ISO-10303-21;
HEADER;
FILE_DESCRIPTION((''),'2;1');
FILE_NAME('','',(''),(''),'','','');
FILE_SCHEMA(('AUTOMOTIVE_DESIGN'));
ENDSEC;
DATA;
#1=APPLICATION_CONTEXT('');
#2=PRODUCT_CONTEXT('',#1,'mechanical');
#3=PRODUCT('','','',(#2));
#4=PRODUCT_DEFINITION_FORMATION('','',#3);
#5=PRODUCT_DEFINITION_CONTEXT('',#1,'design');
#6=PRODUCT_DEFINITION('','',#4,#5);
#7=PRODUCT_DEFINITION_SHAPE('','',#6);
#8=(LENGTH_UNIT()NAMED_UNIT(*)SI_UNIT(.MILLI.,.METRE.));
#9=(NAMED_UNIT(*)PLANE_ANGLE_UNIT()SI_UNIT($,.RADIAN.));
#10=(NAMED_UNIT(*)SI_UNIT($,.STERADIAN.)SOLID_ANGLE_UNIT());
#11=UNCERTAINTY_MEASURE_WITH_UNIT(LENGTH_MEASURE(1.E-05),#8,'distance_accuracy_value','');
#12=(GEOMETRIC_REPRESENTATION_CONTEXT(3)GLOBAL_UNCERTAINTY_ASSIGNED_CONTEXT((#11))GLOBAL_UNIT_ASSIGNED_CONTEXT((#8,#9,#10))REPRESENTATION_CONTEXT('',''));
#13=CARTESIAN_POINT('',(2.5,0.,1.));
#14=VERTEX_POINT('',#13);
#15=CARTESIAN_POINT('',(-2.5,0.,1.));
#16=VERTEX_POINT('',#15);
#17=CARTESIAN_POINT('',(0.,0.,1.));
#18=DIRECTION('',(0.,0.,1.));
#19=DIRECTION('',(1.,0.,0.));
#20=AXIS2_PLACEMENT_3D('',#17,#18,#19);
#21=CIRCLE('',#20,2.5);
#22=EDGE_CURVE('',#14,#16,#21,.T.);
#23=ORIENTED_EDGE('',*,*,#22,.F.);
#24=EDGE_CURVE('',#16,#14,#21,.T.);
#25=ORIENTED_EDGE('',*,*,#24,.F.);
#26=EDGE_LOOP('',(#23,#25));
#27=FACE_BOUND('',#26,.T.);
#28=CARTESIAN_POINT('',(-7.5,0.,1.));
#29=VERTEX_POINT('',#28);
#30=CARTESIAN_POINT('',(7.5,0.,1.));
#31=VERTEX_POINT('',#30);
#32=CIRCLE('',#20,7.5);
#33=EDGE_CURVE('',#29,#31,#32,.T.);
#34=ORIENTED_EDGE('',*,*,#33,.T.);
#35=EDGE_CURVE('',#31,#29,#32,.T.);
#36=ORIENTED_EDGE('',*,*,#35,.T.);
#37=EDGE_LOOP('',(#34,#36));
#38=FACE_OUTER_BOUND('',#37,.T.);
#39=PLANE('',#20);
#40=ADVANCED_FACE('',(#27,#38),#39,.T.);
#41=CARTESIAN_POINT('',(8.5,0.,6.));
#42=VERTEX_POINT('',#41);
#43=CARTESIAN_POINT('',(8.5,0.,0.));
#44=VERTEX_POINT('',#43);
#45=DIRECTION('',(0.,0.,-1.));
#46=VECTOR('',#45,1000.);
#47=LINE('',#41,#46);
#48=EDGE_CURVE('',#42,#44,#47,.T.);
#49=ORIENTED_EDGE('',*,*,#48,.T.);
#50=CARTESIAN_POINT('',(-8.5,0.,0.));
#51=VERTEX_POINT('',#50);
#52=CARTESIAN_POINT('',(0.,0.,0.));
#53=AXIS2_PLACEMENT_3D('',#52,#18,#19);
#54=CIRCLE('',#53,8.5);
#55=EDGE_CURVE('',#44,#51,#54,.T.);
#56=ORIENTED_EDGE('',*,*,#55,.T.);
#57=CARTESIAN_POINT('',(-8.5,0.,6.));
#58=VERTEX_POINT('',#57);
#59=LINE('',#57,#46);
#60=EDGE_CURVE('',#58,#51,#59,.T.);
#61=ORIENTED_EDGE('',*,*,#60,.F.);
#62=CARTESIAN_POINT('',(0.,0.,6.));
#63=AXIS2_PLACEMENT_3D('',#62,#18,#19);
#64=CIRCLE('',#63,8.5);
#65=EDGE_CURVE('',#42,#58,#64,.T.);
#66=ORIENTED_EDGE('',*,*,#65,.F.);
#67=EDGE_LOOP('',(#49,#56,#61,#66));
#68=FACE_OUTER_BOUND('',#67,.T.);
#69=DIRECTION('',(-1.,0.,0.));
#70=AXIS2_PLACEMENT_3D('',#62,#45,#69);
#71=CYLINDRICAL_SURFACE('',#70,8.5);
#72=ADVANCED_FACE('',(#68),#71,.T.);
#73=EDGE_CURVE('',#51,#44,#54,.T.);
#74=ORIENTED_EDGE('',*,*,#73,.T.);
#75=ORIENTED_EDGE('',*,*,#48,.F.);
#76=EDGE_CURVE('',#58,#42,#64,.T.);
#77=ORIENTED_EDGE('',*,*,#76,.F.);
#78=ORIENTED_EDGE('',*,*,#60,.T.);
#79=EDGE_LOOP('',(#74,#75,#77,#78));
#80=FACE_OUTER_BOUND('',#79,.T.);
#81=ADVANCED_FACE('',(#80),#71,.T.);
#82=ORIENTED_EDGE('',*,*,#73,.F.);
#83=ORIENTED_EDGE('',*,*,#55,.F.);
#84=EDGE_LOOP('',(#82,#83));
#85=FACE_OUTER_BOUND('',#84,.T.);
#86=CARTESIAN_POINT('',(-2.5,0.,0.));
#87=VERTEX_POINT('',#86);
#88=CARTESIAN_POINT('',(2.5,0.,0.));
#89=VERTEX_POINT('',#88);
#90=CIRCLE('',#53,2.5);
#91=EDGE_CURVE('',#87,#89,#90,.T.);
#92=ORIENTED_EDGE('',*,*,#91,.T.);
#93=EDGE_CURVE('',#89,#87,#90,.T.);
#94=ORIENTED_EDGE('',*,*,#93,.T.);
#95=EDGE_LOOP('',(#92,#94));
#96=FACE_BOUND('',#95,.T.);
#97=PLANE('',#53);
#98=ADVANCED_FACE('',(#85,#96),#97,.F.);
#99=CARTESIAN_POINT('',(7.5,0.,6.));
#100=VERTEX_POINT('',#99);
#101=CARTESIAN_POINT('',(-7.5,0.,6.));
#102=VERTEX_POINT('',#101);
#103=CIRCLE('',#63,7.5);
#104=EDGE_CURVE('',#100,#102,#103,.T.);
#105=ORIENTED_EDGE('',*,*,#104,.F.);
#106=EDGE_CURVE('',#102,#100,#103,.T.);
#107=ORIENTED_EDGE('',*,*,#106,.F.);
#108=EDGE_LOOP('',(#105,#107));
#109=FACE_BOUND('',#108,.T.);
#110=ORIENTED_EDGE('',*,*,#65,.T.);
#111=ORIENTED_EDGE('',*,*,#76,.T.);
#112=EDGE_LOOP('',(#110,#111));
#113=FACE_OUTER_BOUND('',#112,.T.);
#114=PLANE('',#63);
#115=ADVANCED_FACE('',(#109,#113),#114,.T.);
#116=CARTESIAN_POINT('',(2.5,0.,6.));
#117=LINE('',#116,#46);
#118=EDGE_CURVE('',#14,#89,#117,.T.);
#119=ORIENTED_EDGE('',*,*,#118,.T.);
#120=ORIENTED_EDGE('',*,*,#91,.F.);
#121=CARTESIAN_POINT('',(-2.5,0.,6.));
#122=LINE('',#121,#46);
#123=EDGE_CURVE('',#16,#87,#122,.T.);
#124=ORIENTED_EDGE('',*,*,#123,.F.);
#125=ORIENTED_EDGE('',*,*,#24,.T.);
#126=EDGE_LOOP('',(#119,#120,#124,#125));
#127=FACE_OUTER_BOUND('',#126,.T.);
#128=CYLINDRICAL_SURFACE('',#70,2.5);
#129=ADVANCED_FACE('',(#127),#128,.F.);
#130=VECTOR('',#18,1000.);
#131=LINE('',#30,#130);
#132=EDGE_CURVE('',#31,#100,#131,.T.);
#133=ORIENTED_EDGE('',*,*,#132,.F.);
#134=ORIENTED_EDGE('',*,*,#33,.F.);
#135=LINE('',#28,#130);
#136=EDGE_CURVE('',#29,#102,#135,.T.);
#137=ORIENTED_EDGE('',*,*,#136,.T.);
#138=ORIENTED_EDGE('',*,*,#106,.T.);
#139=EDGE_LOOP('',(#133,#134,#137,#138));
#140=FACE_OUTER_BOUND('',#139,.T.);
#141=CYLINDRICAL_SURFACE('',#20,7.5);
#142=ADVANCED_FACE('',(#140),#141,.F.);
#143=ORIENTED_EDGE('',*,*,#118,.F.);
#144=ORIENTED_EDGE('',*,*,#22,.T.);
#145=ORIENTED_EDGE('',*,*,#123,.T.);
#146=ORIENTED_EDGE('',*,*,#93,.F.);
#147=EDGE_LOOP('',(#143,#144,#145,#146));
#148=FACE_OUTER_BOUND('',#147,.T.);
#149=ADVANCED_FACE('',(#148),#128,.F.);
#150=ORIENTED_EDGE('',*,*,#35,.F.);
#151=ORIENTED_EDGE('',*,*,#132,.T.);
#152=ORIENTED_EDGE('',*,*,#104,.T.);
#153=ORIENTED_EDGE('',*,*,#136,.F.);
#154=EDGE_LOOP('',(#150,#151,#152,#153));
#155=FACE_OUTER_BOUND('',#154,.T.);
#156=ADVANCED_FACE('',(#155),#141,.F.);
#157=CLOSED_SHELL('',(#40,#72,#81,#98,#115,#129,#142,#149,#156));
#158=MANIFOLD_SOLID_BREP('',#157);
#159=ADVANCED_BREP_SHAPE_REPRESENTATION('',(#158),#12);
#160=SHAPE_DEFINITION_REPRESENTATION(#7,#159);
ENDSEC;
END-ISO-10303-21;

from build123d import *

# Parameters (mm, degrees)
SKETCH1_R           = 8.5
SKETCH1_R_2         = 2.5
BOSS_EXTRUDE1_DEPTH = 6
SKETCH2_R           = 7.5
CUT_EXTRUDE1_DEPTH  = 5


with BuildPart() as part:
    # Sketch1 → Boss-Extrude1 (new body)
    with BuildSketch(Plane.XY):
        Circle(SKETCH1_R)
        Circle(SKETCH1_R_2, mode=Mode.SUBTRACT)
    extrude(amount=BOSS_EXTRUDE1_DEPTH)

    # Sketch2 → Cut-Extrude1 (cut)
    with BuildSketch(Plane.XY.offset(6)):
        Circle(SKETCH2_R)
    extrude(amount=-CUT_EXTRUDE1_DEPTH, mode=Mode.SUBTRACT)


solid = part.part
